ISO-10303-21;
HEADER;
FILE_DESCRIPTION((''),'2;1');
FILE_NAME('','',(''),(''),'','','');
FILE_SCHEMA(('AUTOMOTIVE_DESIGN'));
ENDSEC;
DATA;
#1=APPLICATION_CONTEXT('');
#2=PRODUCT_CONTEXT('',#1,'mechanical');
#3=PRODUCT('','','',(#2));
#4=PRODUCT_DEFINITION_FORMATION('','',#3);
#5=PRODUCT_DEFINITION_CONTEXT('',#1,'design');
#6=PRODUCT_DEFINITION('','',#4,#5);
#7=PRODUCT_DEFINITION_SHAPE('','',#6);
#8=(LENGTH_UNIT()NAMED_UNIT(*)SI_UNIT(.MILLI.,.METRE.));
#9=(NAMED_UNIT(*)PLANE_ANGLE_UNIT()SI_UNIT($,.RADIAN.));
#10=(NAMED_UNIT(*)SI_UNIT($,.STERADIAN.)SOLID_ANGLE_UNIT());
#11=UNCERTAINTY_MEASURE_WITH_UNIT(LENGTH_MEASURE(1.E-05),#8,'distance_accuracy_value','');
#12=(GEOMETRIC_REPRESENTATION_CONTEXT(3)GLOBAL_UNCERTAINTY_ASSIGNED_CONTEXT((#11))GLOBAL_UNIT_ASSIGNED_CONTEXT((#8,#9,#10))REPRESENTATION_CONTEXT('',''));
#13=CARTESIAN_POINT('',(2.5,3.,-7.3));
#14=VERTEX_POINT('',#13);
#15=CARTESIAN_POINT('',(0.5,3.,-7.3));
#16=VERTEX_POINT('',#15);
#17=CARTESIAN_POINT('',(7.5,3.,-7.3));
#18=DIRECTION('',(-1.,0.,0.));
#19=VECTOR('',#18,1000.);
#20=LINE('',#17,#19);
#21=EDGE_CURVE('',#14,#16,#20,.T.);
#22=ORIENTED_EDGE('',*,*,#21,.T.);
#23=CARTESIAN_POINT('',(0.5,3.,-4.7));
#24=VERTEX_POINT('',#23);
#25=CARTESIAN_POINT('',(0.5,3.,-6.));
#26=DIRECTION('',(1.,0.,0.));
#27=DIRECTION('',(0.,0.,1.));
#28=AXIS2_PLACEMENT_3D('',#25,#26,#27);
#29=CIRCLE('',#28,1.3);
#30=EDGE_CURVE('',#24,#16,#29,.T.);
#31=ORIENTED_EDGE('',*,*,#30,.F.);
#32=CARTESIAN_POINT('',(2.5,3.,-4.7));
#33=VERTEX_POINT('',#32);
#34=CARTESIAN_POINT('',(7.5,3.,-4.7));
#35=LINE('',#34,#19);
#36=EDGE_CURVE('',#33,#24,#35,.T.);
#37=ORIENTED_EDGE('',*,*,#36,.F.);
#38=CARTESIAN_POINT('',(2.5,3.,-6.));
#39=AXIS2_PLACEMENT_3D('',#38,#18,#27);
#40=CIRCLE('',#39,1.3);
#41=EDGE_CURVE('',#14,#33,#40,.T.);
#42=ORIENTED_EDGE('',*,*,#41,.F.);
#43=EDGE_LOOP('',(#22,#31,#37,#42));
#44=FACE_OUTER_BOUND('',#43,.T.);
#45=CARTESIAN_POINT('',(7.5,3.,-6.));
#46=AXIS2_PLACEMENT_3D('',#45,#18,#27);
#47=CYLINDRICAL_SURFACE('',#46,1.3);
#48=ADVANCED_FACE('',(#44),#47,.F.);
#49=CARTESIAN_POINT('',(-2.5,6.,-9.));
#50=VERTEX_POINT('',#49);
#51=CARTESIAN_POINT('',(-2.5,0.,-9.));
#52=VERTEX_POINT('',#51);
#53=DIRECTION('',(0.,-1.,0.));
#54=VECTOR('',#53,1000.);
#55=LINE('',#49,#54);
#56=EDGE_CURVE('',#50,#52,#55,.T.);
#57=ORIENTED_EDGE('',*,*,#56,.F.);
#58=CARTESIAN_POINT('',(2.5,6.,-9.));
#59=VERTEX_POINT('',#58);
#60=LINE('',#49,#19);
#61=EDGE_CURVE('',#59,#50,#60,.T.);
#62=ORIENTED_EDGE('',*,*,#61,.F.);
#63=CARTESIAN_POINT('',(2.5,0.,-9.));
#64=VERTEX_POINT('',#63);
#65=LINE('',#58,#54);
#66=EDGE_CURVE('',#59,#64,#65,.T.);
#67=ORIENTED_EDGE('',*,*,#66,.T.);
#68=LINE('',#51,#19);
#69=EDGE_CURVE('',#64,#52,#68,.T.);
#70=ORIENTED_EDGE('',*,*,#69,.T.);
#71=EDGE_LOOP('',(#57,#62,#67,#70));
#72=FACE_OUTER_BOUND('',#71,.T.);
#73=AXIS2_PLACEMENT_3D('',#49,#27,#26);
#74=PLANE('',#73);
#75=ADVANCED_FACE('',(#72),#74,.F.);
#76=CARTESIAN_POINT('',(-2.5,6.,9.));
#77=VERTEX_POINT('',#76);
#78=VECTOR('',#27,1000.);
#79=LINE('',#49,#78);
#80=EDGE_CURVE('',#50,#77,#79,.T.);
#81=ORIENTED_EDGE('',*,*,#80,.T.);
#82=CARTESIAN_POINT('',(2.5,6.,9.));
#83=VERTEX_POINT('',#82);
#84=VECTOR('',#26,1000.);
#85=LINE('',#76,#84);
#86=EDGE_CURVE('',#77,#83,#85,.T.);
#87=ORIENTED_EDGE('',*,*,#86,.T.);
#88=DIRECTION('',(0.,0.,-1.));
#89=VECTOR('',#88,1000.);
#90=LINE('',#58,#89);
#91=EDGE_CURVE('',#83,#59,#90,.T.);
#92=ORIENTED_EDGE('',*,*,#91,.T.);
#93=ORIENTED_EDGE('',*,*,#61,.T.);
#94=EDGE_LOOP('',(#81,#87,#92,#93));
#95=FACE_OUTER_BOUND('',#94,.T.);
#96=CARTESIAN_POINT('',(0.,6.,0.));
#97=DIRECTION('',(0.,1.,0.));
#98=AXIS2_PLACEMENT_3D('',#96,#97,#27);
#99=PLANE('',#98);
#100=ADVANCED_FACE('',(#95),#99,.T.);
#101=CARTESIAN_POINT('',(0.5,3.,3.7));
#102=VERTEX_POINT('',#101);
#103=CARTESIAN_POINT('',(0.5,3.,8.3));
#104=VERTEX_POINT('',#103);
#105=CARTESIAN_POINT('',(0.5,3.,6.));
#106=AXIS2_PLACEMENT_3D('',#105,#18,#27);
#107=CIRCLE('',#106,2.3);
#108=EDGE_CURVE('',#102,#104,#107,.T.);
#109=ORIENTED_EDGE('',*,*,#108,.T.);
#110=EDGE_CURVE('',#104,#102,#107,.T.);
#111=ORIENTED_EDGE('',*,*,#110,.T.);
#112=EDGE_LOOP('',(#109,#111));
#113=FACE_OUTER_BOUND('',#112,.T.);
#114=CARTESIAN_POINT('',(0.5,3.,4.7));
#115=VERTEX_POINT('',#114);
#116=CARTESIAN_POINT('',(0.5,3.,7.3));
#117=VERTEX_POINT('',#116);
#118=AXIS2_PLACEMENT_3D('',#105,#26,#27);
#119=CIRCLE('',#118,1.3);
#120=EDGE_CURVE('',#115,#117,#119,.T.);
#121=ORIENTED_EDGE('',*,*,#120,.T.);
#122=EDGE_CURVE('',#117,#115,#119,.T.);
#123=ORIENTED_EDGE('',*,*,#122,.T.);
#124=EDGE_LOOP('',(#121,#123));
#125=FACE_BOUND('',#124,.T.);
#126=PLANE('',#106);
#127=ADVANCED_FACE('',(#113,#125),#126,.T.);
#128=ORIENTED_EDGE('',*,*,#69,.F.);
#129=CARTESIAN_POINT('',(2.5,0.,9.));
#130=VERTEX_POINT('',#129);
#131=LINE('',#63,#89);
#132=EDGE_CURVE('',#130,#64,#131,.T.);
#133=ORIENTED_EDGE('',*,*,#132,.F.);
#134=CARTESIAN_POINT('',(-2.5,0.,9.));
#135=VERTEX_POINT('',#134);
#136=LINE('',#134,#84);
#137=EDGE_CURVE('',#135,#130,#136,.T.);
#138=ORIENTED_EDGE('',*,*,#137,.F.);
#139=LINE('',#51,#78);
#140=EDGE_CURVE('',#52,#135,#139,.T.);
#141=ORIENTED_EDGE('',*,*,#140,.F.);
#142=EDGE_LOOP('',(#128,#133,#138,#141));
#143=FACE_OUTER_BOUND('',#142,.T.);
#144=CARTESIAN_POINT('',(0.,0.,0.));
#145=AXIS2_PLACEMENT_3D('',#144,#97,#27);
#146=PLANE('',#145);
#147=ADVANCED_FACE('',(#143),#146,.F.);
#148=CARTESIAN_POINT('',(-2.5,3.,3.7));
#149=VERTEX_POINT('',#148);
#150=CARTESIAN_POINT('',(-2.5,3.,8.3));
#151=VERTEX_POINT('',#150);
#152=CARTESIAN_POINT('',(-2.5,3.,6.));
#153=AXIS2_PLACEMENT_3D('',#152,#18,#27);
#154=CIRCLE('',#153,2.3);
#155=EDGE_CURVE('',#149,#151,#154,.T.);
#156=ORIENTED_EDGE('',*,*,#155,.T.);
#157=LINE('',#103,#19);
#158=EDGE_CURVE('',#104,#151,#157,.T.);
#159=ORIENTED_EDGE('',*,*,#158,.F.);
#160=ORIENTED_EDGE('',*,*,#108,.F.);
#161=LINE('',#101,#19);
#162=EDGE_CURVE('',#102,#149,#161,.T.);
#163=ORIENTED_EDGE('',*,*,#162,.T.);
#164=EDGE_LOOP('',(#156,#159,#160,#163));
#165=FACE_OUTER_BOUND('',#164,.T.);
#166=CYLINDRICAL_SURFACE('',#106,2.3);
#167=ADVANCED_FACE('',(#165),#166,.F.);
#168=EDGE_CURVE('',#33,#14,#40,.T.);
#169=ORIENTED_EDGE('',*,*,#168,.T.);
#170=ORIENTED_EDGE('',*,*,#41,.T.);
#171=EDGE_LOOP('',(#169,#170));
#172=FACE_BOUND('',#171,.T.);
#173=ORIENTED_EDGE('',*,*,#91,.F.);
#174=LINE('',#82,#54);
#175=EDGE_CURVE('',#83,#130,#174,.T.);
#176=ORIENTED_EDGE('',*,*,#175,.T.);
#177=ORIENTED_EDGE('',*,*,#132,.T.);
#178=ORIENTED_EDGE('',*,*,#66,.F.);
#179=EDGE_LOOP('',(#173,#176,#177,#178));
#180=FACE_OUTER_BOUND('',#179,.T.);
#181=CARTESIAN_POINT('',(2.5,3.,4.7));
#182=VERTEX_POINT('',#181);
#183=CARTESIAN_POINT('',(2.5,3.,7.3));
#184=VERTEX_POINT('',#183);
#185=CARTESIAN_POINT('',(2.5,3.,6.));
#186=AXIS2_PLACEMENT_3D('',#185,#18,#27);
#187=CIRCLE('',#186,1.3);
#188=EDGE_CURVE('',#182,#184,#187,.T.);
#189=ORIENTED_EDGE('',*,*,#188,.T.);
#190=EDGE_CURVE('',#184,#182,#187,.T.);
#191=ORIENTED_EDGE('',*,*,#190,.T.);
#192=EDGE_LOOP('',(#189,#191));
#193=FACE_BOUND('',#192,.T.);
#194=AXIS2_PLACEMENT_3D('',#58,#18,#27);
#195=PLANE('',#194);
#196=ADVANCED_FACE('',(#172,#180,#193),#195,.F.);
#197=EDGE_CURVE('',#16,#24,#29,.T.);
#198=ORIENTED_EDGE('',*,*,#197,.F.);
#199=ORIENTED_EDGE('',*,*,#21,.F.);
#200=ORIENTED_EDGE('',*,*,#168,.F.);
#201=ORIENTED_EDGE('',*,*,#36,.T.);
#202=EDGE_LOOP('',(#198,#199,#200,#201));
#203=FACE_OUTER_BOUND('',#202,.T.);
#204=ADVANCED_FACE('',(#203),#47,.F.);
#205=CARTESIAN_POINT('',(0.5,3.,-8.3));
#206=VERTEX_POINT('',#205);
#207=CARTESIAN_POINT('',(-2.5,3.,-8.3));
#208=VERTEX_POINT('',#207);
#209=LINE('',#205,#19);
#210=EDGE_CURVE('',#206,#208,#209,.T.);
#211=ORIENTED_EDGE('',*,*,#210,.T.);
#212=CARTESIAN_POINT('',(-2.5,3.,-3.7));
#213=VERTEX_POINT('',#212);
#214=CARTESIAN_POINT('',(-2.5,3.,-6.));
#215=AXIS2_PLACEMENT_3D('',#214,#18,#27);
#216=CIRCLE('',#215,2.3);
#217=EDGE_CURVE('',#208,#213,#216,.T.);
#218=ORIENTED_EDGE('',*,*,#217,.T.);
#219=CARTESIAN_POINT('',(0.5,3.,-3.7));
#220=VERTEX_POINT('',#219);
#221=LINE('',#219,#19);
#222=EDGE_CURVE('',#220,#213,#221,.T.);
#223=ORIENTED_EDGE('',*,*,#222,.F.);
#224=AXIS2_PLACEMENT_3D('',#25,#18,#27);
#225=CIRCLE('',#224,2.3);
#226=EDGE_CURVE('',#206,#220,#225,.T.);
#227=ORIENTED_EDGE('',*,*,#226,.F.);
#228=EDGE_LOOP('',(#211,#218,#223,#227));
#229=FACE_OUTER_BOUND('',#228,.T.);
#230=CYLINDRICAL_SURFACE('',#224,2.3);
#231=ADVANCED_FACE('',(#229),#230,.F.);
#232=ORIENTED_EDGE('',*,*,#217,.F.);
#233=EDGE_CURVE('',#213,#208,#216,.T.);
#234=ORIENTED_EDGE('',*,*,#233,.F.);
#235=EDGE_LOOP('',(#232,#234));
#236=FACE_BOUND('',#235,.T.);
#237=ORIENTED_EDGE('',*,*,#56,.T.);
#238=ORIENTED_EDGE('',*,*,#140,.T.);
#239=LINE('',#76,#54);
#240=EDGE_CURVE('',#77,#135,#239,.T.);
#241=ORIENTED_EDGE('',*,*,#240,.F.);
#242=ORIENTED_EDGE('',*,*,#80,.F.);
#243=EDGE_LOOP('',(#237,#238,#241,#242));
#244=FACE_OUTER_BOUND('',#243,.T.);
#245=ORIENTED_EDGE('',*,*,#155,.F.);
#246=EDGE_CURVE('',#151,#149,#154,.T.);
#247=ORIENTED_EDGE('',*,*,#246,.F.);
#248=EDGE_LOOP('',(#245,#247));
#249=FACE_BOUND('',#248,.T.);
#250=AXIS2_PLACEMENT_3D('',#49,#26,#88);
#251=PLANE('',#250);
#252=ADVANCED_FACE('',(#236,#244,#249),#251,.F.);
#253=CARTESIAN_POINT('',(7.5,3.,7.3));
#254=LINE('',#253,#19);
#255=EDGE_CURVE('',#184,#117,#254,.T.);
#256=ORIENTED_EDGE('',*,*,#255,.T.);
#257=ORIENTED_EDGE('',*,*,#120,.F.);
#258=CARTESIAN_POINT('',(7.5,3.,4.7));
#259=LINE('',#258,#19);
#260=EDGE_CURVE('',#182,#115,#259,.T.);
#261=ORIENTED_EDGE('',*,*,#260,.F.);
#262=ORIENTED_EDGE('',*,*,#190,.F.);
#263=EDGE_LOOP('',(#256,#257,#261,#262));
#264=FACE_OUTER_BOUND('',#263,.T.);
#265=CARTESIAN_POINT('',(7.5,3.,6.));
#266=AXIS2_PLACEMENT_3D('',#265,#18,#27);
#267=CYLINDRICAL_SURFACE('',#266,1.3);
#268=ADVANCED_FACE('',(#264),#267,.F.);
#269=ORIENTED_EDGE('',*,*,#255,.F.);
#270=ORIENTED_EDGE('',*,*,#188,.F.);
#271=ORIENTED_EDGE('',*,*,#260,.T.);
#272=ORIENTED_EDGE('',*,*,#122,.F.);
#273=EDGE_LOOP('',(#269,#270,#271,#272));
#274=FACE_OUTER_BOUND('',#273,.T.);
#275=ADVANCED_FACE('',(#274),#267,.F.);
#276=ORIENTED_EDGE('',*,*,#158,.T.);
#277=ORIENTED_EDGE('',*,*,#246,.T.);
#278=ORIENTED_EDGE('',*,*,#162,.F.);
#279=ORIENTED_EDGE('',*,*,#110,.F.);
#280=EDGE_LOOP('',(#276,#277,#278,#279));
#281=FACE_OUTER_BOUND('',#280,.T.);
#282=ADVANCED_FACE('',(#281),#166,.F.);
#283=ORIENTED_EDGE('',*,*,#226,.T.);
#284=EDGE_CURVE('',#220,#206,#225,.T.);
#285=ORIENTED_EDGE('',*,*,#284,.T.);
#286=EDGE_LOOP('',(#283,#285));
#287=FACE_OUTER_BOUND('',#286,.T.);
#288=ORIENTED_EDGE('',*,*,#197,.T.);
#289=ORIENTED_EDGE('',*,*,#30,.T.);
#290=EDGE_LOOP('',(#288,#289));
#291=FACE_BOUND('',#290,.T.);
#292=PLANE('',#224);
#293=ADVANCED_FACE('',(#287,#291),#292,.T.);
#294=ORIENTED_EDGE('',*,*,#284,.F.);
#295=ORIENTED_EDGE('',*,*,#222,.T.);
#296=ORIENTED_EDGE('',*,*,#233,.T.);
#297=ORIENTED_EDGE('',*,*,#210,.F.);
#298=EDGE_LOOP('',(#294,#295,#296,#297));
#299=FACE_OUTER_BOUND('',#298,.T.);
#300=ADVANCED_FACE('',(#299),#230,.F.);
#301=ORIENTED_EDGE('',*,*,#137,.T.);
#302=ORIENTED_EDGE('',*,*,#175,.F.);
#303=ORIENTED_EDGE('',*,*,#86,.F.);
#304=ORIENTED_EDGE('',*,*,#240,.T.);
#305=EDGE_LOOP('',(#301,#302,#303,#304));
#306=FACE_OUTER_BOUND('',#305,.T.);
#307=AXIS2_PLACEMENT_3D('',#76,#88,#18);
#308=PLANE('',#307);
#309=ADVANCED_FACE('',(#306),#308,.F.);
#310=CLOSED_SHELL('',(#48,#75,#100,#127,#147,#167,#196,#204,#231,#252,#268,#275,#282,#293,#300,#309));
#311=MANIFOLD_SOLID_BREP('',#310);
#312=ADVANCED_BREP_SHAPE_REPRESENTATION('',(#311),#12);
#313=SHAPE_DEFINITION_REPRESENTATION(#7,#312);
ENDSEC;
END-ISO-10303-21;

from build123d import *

# Parameters (mm, degrees)
SKETCH1_W           = 5
SKETCH1_H           = 18
BOSS_EXTRUDE1_DEPTH = 6
SKETCH2_R           = 1.3
CUT_EXTRUDE1_DEPTH  = 10
SKETCH3_R           = 2.3
CUT_EXTRUDE2_DEPTH  = 3


with BuildPart() as part:
    # Sketch1 → Boss-Extrude1 (new body)
    with BuildSketch(Plane(origin=(0, 0, 0), x_dir=(1, 0, 0), z_dir=(0, 1, 0))):
        Rectangle(SKETCH1_W, SKETCH1_H)
    extrude(amount=BOSS_EXTRUDE1_DEPTH)

    # Sketch2 → Cut-Extrude1 (cut)
    with BuildSketch(Plane.ZY.offset(2.5)):
        with Locations((6, 3)):
            Circle(SKETCH2_R)
        with Locations((-6, 3)):
            Circle(SKETCH2_R)
    extrude(amount=-CUT_EXTRUDE1_DEPTH, mode=Mode.SUBTRACT)

    # Sketch3 → Cut-Extrude2 (cut)
    with BuildSketch(Plane.ZY.offset(2.5)):
        with Locations((-6, 3)):
            Circle(SKETCH3_R)
        with Locations((6, 3)):
            Circle(SKETCH3_R)
    extrude(amount=-CUT_EXTRUDE2_DEPTH, mode=Mode.SUBTRACT)


solid = part.part
